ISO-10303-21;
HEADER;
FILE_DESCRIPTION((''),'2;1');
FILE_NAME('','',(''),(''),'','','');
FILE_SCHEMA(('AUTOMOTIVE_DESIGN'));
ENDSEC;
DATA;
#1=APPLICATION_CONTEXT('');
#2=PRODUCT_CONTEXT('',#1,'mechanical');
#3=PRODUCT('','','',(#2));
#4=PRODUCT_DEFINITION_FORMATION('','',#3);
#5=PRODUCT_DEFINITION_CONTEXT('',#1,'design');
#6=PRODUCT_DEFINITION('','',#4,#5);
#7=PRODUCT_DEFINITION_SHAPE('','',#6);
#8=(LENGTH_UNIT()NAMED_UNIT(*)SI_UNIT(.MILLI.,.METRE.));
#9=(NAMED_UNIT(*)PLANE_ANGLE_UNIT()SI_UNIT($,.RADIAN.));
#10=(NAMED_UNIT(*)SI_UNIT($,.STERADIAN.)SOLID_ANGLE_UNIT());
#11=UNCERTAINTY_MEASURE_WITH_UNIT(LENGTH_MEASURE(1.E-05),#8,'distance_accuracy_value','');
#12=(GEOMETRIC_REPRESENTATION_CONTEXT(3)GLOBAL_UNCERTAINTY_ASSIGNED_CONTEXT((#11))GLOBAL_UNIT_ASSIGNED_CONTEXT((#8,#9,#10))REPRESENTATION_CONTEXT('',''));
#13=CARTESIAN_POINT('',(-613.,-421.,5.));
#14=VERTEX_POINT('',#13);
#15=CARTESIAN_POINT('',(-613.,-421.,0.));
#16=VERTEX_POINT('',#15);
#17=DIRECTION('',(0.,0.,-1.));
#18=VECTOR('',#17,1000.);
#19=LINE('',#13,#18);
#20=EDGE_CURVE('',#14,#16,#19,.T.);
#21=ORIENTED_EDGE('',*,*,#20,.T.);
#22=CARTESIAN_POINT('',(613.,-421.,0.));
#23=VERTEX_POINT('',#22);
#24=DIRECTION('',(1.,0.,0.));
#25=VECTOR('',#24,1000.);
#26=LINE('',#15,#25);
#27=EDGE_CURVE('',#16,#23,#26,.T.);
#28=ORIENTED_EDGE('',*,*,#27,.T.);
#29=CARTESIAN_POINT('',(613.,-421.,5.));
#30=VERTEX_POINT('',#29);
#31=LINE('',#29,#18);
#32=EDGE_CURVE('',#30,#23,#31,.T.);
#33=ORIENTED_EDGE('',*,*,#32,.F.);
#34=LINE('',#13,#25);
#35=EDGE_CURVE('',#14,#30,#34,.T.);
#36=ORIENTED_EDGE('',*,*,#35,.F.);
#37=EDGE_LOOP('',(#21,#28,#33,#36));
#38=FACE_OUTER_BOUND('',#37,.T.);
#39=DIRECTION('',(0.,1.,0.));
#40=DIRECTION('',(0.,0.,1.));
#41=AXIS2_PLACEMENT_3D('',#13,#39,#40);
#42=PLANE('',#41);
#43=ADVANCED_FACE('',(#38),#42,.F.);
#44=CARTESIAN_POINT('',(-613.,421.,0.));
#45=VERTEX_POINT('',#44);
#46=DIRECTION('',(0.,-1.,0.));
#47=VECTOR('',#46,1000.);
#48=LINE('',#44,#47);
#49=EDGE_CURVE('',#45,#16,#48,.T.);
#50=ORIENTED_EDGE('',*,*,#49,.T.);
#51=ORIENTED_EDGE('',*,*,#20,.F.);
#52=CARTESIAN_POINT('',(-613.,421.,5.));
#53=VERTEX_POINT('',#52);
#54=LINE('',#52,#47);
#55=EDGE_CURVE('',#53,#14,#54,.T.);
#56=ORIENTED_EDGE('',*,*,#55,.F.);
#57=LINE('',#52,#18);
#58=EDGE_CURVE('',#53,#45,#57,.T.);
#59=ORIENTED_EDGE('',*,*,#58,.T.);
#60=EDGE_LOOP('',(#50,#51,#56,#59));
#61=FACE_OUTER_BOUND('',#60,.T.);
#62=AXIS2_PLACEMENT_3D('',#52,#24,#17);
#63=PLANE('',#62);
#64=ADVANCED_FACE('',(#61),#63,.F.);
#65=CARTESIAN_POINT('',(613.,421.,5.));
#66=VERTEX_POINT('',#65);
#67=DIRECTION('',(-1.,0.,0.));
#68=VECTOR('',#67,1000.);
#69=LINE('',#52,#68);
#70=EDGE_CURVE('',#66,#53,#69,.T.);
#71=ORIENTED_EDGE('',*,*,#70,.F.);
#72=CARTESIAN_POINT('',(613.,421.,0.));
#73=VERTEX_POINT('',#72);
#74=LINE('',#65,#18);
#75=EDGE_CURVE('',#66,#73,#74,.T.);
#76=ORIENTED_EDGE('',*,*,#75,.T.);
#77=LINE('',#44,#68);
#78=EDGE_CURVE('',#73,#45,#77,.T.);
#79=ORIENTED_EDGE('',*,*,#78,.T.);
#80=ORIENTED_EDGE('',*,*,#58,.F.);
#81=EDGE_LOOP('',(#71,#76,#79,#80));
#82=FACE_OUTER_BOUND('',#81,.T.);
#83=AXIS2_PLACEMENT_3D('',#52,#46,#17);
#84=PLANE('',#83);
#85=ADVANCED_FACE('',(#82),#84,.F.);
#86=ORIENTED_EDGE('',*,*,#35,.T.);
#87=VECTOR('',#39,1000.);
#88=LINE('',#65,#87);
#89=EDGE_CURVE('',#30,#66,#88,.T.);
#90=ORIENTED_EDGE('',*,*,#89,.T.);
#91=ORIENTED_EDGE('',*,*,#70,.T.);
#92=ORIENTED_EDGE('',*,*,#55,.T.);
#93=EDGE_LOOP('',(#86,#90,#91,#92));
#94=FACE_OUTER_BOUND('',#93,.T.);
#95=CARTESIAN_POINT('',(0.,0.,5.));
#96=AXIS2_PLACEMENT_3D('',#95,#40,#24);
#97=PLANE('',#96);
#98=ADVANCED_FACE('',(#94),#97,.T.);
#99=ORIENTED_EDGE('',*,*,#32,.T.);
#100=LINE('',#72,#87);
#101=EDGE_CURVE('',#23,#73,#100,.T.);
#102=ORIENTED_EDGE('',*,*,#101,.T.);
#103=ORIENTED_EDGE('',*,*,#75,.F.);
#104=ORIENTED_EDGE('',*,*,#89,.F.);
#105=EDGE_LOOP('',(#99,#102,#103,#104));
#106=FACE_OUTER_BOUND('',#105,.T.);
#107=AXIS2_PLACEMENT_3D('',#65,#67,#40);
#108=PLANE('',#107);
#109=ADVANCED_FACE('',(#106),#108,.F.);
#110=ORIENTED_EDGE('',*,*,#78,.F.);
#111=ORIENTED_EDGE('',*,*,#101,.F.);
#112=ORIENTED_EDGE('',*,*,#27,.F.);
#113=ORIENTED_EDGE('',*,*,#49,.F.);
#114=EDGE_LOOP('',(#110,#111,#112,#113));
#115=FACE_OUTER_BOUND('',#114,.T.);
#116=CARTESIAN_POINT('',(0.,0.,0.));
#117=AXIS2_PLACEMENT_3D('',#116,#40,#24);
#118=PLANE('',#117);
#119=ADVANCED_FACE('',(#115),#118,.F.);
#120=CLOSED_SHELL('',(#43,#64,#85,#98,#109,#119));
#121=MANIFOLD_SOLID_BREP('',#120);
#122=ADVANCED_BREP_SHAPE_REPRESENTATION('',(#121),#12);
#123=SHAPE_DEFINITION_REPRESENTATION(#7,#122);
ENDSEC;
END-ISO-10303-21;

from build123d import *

# Parameters (mm, degrees)
SKETCH_1_W      = 1226
SKETCH_1_H      = 842
EXTRUDE_1_DEPTH = 5


with BuildPart() as part:
    # 草图1 → 凸台-拉伸1 (new body)
    with BuildSketch(Plane.XY):
        Rectangle(SKETCH_1_W, SKETCH_1_H)
    extrude(amount=EXTRUDE_1_DEPTH)


solid = part.part
